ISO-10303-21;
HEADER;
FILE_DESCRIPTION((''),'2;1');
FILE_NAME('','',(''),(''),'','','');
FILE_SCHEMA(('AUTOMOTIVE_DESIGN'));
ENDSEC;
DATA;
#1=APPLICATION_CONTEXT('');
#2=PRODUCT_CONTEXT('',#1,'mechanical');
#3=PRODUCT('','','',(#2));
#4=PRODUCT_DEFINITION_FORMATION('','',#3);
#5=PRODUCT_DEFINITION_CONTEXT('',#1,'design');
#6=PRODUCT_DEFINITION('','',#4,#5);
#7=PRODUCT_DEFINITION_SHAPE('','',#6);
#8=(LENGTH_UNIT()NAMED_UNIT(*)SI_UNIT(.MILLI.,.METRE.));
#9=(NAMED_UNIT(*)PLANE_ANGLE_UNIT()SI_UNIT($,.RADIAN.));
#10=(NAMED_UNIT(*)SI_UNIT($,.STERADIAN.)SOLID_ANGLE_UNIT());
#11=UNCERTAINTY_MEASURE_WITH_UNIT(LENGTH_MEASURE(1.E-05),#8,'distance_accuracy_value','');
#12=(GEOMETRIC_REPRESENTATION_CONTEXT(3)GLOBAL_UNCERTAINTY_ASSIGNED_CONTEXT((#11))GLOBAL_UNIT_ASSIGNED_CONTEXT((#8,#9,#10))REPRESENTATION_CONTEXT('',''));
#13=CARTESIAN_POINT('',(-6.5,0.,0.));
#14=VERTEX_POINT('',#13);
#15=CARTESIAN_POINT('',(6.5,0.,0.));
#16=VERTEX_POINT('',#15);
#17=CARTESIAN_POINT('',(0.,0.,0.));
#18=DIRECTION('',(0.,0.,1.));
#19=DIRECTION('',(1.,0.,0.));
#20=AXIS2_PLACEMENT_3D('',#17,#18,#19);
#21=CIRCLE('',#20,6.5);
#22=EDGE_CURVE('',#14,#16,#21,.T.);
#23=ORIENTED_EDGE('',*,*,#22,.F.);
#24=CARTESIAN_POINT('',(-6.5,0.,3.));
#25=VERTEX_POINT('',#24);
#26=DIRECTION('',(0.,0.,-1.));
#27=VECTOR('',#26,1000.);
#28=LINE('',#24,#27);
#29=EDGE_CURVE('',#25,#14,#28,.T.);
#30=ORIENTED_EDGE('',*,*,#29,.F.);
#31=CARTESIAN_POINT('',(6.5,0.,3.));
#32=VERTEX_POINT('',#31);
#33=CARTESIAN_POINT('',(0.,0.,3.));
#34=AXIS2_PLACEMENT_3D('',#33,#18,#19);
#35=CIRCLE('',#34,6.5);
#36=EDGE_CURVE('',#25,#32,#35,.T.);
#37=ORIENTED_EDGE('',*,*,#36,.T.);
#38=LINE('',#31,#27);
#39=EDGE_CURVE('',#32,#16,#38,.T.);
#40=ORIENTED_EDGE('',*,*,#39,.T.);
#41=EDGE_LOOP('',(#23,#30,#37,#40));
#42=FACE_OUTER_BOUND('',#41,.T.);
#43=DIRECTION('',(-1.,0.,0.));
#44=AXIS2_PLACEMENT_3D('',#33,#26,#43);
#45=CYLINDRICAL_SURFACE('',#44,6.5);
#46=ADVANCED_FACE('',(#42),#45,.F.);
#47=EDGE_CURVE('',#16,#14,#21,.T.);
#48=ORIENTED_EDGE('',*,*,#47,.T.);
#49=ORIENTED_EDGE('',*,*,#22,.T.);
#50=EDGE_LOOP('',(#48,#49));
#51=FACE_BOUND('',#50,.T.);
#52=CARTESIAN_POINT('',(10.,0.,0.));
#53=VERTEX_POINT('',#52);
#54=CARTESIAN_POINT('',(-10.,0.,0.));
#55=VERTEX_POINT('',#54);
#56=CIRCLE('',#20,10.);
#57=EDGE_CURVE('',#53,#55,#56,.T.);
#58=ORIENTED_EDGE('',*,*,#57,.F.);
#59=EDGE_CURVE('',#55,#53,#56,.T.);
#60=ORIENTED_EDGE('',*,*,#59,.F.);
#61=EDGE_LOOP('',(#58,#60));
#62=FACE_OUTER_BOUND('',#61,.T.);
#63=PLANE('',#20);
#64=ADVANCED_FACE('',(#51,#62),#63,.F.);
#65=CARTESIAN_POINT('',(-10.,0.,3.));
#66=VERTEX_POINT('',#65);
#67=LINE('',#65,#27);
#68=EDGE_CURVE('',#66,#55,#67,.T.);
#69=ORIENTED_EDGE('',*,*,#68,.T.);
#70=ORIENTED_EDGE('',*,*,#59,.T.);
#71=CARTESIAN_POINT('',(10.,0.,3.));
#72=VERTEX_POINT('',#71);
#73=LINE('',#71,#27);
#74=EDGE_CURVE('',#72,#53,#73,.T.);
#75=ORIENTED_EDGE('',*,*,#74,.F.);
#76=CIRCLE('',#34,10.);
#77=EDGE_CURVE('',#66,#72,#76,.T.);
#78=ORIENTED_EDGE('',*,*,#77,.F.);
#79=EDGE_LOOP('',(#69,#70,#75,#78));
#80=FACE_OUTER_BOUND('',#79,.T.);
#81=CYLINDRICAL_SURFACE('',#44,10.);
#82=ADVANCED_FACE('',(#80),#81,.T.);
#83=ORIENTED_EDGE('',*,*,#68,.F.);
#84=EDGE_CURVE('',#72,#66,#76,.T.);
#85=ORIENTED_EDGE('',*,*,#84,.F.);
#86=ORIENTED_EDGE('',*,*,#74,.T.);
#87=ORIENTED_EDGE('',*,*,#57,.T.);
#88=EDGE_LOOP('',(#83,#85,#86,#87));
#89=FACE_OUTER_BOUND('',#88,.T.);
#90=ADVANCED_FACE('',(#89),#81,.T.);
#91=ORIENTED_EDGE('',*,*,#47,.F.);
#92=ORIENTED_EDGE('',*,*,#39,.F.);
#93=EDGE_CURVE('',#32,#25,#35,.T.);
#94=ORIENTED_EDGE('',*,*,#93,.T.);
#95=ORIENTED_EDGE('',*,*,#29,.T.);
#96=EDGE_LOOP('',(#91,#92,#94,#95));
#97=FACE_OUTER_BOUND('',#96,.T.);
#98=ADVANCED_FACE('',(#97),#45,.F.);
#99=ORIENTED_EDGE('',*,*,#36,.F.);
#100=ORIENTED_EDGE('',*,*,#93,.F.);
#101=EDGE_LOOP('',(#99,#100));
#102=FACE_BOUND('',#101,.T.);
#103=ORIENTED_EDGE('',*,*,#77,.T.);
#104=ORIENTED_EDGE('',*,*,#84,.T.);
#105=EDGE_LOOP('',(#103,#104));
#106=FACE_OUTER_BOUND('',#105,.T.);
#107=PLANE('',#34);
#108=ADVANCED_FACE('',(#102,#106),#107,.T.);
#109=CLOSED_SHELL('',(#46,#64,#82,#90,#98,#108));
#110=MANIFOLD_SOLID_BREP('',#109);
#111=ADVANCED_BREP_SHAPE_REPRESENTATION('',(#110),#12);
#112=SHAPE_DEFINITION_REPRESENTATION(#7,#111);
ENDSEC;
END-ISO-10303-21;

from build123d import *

# Parameters (mm, degrees)
WASHER_PROFILE_20X_13_R   = 10
WASHER_PROFILE_20X_13_R_2 = 6.5
WASHER_BODY_3MM_DEPTH     = 3


with BuildPart() as part:
    # Washer Profile Ø20xØ13 → Washer Body 3mm (new body)
    with BuildSketch(Plane.XY):
        Circle(WASHER_PROFILE_20X_13_R)
        Circle(WASHER_PROFILE_20X_13_R_2, mode=Mode.SUBTRACT)
    extrude(amount=WASHER_BODY_3MM_DEPTH)


solid = part.part
